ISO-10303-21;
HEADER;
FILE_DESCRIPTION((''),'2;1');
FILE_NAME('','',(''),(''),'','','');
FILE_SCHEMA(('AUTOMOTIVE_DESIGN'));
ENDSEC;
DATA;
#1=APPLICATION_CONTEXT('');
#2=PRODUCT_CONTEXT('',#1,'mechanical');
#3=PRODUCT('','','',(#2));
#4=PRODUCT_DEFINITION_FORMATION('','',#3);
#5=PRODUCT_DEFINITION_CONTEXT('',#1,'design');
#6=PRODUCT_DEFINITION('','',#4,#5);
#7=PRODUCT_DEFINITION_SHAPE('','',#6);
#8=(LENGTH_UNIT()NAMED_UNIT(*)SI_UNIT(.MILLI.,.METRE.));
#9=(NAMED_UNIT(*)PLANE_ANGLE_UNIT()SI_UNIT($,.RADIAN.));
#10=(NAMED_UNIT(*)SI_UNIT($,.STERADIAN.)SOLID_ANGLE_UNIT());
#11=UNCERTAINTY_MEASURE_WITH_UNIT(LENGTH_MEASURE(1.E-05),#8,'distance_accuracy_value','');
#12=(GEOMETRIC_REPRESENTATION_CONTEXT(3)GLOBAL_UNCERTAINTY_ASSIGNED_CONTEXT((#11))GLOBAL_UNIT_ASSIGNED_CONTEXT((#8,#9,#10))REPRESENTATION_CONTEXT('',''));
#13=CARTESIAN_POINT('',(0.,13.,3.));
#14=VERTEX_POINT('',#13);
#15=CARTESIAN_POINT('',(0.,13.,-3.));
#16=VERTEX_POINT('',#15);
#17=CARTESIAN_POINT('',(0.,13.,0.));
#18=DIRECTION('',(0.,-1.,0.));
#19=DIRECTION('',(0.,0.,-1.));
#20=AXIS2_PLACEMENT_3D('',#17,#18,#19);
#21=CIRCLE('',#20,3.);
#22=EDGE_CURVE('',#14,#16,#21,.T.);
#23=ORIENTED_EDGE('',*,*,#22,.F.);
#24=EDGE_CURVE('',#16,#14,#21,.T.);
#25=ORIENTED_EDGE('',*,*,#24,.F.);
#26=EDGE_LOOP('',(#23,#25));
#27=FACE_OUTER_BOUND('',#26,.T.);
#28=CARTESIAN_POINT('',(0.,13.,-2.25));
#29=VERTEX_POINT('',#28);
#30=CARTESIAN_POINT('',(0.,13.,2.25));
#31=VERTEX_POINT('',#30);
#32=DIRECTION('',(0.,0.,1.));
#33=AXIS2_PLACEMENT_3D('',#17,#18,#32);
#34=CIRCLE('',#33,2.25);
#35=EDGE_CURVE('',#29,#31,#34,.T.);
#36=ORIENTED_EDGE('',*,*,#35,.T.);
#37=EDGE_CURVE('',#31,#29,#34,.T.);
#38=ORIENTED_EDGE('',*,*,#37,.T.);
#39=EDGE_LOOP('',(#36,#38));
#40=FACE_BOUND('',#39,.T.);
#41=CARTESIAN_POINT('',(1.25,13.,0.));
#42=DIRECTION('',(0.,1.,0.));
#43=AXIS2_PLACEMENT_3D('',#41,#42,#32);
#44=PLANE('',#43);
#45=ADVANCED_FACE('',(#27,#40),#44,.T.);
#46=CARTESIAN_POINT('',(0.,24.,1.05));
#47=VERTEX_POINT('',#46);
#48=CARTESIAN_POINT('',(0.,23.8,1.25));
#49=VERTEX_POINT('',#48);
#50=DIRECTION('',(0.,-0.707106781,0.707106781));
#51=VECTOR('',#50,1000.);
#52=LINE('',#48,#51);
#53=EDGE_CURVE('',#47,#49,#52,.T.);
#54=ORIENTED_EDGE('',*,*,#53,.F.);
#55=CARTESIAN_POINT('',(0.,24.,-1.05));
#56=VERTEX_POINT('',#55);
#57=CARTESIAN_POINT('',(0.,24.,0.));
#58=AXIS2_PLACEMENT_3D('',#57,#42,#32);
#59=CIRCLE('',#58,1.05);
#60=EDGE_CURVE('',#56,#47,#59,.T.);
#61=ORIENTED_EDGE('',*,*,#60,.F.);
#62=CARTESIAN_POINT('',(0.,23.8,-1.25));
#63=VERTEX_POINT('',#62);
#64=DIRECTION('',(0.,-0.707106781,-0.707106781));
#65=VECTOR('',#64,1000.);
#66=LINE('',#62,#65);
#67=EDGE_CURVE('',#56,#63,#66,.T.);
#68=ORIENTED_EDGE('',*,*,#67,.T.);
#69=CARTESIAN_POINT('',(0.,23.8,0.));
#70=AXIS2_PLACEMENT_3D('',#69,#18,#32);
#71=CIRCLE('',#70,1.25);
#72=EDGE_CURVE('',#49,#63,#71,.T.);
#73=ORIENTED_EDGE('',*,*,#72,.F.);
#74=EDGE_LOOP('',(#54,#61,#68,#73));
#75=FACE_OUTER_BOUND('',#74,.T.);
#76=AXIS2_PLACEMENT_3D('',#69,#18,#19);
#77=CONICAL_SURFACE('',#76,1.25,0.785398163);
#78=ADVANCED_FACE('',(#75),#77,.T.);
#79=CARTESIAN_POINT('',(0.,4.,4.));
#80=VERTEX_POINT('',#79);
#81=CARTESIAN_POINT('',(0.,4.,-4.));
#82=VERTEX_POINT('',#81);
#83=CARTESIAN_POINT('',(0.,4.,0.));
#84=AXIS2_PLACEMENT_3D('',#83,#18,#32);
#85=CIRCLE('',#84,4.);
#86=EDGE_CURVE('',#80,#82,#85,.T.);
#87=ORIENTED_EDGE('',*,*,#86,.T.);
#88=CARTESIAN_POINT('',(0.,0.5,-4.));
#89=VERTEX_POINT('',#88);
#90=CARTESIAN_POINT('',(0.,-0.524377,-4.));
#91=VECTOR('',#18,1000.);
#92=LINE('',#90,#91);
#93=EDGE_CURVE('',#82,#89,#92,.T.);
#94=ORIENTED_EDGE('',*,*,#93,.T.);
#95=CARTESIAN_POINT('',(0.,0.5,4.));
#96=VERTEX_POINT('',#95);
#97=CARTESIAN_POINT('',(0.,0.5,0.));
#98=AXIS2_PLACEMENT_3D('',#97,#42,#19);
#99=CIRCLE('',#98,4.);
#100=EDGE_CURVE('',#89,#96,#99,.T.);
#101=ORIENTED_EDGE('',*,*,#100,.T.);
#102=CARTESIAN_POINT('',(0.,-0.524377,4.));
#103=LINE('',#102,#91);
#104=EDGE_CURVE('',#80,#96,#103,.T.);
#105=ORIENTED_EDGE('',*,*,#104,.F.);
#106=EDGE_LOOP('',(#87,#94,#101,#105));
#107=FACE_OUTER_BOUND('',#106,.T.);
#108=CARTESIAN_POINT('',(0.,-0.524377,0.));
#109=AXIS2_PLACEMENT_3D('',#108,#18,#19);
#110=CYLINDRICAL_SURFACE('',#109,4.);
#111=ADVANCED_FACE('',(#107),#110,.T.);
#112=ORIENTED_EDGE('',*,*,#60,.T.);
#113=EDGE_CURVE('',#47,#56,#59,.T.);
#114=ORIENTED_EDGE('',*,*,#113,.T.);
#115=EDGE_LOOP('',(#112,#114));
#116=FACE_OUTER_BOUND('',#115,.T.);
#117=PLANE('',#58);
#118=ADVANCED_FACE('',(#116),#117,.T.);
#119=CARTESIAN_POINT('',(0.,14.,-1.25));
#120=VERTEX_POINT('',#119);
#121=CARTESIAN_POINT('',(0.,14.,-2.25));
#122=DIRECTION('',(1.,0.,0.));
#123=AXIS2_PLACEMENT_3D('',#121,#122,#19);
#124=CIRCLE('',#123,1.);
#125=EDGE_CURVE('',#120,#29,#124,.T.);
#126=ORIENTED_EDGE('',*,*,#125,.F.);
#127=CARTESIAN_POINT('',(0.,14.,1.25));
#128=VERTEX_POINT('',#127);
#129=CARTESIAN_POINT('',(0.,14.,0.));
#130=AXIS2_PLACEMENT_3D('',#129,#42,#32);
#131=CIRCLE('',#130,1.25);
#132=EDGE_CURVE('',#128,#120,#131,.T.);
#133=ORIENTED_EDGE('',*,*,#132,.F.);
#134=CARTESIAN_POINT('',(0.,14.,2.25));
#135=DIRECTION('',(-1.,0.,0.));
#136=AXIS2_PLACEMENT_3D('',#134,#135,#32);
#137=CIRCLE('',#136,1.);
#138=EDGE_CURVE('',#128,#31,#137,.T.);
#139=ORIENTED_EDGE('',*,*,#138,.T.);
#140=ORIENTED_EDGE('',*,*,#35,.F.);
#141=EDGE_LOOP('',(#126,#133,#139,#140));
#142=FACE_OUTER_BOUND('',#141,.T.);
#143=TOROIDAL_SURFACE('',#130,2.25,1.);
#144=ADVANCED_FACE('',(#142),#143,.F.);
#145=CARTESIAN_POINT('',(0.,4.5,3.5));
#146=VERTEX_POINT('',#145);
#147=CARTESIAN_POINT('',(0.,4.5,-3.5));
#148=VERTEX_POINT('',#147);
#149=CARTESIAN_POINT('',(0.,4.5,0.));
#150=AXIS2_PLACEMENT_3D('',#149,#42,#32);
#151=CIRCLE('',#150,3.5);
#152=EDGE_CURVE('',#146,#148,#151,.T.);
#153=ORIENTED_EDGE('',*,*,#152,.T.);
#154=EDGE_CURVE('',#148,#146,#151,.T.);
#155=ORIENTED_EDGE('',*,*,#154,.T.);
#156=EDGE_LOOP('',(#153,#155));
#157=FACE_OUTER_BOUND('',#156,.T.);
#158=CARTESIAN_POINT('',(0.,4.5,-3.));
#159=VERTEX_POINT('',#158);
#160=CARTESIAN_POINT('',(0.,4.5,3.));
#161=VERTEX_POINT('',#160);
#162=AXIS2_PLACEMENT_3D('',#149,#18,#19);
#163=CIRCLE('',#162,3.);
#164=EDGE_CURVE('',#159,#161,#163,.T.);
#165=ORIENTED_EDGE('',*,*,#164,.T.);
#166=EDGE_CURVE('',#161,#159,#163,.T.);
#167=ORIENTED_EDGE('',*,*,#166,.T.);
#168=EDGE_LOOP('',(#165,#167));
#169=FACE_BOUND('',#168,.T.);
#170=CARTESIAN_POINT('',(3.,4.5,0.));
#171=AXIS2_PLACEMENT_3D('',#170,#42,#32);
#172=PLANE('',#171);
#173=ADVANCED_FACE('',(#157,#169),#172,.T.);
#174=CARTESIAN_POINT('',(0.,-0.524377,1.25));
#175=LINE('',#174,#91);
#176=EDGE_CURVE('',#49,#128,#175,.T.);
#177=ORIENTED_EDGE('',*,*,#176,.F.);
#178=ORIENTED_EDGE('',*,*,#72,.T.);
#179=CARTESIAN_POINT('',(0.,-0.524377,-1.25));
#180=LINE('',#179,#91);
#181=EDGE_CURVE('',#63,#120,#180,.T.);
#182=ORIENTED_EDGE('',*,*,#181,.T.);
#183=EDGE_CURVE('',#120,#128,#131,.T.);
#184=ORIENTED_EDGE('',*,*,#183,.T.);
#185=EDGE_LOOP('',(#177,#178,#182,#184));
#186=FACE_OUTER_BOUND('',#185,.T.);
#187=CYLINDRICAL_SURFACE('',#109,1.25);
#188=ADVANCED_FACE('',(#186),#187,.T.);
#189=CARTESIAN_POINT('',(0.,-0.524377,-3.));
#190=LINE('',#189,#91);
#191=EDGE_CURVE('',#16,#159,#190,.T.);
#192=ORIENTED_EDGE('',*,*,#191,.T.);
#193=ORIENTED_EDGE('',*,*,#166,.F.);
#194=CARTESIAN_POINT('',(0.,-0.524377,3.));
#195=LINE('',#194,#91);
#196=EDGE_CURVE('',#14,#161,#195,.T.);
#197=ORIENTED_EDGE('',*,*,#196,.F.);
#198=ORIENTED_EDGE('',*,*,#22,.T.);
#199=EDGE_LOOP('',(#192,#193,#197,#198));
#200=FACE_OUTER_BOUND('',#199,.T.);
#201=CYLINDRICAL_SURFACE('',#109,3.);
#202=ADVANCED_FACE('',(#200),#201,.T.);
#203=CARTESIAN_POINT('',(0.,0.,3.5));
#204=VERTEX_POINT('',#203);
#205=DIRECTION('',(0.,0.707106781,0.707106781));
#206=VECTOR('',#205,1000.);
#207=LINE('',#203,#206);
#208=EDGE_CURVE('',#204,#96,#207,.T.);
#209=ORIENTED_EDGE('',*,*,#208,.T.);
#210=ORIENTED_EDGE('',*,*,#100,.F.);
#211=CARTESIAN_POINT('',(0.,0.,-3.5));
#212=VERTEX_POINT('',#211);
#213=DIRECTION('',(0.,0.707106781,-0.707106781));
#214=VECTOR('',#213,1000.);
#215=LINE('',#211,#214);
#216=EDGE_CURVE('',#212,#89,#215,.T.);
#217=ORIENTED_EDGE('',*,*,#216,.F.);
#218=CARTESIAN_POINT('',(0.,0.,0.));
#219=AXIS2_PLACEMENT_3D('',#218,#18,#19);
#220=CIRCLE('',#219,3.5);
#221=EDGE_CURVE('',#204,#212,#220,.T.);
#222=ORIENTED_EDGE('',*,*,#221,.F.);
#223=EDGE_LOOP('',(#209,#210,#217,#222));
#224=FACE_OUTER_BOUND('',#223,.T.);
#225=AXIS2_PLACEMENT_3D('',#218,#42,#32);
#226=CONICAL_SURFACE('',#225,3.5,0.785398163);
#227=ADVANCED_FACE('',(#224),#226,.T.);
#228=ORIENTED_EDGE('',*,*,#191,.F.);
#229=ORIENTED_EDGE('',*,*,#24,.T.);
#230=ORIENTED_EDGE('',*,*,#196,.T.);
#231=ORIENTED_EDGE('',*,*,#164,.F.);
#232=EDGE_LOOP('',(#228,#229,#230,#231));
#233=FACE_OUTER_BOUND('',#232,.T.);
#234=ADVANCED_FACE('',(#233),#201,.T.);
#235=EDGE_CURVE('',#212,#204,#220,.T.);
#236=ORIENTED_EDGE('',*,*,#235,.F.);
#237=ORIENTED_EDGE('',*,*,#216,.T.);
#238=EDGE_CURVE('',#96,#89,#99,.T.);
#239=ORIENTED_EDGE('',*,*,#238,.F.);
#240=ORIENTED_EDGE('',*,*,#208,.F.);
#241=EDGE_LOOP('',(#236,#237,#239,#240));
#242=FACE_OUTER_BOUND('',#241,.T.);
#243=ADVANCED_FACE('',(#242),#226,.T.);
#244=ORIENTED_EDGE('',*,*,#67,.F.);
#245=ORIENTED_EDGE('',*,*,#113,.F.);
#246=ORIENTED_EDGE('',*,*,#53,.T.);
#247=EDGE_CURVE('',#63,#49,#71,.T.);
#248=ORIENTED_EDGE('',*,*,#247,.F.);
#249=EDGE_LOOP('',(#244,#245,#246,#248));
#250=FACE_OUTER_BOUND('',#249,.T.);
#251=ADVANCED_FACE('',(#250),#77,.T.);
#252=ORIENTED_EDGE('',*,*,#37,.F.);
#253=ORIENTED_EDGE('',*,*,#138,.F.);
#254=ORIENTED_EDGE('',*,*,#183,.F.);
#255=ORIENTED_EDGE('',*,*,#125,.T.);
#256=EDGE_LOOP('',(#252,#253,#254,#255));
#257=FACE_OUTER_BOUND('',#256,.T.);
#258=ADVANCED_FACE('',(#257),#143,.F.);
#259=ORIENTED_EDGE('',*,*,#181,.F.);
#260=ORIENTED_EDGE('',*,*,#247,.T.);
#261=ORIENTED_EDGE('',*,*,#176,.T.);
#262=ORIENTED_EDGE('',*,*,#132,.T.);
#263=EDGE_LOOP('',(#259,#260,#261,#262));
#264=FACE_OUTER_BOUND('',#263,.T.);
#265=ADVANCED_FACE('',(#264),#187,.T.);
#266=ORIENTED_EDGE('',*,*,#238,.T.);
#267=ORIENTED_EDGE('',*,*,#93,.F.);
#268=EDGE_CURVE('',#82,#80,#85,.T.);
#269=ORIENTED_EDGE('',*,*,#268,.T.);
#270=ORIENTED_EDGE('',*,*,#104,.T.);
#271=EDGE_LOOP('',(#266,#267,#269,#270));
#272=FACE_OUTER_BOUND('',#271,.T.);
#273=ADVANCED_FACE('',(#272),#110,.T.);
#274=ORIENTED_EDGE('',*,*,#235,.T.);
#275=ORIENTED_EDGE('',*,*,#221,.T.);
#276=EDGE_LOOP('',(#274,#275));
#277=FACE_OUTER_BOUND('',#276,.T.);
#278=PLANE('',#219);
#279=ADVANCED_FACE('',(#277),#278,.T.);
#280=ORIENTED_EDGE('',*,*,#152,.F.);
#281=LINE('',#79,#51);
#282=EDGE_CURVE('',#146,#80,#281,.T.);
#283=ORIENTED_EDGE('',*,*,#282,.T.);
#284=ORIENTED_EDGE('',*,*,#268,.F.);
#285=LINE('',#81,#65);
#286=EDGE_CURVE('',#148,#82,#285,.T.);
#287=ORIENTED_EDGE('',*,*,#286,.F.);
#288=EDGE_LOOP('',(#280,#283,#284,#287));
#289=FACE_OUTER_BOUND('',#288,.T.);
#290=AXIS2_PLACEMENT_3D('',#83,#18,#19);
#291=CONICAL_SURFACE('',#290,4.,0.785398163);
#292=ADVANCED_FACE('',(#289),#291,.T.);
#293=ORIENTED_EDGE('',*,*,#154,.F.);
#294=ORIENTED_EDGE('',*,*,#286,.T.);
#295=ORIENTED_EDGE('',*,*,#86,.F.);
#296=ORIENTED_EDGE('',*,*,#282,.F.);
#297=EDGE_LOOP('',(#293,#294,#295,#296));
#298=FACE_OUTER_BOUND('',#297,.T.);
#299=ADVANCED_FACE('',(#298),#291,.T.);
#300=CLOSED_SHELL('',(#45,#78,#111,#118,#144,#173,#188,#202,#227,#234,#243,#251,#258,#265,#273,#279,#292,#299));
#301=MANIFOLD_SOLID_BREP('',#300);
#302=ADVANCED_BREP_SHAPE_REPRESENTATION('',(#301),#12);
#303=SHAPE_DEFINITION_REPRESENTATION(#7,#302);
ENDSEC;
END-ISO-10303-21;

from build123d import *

# Parameters (mm, degrees)
CHAMFER_1_SIZE = 0.5
FILLET_1_R     = 1
CHAMFER_2_SIZE = 0.2


with BuildPart() as part:
    # 草图1 → 旋转1 (revolve)
    with BuildSketch(Plane.XY, mode=Mode.PRIVATE) as revolve_1_sk:
        Polygon((1.25, 24), (1.25, 13), (3, 13), (3, 4.5), (4, 4.5), (4, 0), (0, 0), (0, 24), align=None)
    revolve(revolve_1_sk.sketch.rotate(Axis((0, -0.524377328, 0), (0, 1, 0)), 90), axis=Axis((0, -0.524377328, 0), (0, 1, 0)))

    # 倒角1
    chamfer_1_edges = [part.edges().sort_by_distance(p)[0] for p in [
        (0, 0, 4),
        (0, 4.5, 4),
    ]]
    chamfer(chamfer_1_edges, length=CHAMFER_1_SIZE)

    # 圆角1
    fillet_1_edges = [part.edges().sort_by_distance(p)[0] for p in [
        (0, 13, 1.25),
    ]]
    fillet(fillet_1_edges, radius=FILLET_1_R)

    # 倒角2
    chamfer_2_edges = [part.edges().sort_by_distance(p)[0] for p in [
        (0, 24, 1.25),
    ]]
    chamfer(chamfer_2_edges, length=CHAMFER_2_SIZE)


solid = part.part
